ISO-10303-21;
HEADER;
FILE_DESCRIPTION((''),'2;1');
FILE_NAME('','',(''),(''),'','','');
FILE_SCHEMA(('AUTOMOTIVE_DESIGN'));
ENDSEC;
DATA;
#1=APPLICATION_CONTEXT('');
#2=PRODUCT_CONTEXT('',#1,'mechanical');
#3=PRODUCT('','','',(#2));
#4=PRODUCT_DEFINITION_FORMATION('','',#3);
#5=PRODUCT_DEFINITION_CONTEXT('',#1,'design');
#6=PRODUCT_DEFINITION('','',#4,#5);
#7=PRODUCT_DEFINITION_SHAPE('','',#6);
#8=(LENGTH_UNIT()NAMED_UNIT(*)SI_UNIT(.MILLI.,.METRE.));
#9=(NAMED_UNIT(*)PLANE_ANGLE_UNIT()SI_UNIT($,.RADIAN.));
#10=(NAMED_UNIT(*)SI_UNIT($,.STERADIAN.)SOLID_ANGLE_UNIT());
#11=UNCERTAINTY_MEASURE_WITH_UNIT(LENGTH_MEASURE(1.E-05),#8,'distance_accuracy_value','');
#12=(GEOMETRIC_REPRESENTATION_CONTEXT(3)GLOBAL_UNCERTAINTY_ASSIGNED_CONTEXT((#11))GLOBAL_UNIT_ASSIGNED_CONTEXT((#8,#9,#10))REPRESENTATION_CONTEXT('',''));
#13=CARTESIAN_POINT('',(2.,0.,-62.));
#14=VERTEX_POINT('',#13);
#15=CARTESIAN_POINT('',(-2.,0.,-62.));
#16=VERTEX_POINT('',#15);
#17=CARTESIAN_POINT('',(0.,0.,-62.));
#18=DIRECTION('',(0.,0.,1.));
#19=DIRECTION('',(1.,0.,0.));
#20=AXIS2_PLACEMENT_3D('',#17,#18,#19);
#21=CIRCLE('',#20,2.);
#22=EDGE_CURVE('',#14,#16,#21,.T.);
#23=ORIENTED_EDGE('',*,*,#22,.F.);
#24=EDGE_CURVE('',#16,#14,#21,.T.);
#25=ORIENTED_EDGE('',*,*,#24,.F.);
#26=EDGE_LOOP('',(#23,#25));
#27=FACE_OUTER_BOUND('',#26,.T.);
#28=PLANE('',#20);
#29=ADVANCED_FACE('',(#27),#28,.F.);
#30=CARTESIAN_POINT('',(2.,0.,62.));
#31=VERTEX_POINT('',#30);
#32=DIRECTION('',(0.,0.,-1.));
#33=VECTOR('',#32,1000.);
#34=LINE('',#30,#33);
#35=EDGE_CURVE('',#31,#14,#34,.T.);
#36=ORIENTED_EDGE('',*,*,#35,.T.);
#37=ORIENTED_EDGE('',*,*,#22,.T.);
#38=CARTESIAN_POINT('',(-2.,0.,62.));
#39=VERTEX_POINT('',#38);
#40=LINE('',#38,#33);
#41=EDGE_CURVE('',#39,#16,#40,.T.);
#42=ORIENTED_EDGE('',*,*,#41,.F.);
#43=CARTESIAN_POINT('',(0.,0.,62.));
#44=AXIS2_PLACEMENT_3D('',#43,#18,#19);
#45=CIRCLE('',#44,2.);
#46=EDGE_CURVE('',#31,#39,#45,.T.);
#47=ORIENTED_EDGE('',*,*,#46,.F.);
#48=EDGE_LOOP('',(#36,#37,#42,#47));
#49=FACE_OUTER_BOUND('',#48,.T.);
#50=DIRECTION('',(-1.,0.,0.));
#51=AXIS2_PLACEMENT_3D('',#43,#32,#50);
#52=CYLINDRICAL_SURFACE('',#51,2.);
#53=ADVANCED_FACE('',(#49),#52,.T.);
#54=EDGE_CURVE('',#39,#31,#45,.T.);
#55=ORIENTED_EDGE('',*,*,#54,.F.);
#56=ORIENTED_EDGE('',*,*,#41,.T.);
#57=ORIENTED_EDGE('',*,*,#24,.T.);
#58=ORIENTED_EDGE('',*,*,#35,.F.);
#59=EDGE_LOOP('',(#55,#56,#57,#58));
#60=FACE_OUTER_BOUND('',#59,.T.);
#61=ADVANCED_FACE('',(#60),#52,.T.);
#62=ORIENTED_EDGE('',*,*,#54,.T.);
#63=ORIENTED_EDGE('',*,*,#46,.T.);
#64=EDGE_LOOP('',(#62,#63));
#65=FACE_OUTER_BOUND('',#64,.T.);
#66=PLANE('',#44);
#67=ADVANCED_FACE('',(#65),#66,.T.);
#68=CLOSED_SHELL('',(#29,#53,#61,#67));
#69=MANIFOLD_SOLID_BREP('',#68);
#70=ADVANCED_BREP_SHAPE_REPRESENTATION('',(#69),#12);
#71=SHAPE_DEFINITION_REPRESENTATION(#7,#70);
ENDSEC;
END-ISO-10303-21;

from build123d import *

# Parameters (mm, degrees)
SKETCH1_R           = 2
BOSS_EXTRUDE1_DEPTH = 62


with BuildPart() as part:
    # Sketch1 → Boss-Extrude1 (new, symmetric)
    with BuildSketch(Plane.XY):
        Circle(SKETCH1_R)
    extrude(amount=BOSS_EXTRUDE1_DEPTH, both=True)


solid = part.part
